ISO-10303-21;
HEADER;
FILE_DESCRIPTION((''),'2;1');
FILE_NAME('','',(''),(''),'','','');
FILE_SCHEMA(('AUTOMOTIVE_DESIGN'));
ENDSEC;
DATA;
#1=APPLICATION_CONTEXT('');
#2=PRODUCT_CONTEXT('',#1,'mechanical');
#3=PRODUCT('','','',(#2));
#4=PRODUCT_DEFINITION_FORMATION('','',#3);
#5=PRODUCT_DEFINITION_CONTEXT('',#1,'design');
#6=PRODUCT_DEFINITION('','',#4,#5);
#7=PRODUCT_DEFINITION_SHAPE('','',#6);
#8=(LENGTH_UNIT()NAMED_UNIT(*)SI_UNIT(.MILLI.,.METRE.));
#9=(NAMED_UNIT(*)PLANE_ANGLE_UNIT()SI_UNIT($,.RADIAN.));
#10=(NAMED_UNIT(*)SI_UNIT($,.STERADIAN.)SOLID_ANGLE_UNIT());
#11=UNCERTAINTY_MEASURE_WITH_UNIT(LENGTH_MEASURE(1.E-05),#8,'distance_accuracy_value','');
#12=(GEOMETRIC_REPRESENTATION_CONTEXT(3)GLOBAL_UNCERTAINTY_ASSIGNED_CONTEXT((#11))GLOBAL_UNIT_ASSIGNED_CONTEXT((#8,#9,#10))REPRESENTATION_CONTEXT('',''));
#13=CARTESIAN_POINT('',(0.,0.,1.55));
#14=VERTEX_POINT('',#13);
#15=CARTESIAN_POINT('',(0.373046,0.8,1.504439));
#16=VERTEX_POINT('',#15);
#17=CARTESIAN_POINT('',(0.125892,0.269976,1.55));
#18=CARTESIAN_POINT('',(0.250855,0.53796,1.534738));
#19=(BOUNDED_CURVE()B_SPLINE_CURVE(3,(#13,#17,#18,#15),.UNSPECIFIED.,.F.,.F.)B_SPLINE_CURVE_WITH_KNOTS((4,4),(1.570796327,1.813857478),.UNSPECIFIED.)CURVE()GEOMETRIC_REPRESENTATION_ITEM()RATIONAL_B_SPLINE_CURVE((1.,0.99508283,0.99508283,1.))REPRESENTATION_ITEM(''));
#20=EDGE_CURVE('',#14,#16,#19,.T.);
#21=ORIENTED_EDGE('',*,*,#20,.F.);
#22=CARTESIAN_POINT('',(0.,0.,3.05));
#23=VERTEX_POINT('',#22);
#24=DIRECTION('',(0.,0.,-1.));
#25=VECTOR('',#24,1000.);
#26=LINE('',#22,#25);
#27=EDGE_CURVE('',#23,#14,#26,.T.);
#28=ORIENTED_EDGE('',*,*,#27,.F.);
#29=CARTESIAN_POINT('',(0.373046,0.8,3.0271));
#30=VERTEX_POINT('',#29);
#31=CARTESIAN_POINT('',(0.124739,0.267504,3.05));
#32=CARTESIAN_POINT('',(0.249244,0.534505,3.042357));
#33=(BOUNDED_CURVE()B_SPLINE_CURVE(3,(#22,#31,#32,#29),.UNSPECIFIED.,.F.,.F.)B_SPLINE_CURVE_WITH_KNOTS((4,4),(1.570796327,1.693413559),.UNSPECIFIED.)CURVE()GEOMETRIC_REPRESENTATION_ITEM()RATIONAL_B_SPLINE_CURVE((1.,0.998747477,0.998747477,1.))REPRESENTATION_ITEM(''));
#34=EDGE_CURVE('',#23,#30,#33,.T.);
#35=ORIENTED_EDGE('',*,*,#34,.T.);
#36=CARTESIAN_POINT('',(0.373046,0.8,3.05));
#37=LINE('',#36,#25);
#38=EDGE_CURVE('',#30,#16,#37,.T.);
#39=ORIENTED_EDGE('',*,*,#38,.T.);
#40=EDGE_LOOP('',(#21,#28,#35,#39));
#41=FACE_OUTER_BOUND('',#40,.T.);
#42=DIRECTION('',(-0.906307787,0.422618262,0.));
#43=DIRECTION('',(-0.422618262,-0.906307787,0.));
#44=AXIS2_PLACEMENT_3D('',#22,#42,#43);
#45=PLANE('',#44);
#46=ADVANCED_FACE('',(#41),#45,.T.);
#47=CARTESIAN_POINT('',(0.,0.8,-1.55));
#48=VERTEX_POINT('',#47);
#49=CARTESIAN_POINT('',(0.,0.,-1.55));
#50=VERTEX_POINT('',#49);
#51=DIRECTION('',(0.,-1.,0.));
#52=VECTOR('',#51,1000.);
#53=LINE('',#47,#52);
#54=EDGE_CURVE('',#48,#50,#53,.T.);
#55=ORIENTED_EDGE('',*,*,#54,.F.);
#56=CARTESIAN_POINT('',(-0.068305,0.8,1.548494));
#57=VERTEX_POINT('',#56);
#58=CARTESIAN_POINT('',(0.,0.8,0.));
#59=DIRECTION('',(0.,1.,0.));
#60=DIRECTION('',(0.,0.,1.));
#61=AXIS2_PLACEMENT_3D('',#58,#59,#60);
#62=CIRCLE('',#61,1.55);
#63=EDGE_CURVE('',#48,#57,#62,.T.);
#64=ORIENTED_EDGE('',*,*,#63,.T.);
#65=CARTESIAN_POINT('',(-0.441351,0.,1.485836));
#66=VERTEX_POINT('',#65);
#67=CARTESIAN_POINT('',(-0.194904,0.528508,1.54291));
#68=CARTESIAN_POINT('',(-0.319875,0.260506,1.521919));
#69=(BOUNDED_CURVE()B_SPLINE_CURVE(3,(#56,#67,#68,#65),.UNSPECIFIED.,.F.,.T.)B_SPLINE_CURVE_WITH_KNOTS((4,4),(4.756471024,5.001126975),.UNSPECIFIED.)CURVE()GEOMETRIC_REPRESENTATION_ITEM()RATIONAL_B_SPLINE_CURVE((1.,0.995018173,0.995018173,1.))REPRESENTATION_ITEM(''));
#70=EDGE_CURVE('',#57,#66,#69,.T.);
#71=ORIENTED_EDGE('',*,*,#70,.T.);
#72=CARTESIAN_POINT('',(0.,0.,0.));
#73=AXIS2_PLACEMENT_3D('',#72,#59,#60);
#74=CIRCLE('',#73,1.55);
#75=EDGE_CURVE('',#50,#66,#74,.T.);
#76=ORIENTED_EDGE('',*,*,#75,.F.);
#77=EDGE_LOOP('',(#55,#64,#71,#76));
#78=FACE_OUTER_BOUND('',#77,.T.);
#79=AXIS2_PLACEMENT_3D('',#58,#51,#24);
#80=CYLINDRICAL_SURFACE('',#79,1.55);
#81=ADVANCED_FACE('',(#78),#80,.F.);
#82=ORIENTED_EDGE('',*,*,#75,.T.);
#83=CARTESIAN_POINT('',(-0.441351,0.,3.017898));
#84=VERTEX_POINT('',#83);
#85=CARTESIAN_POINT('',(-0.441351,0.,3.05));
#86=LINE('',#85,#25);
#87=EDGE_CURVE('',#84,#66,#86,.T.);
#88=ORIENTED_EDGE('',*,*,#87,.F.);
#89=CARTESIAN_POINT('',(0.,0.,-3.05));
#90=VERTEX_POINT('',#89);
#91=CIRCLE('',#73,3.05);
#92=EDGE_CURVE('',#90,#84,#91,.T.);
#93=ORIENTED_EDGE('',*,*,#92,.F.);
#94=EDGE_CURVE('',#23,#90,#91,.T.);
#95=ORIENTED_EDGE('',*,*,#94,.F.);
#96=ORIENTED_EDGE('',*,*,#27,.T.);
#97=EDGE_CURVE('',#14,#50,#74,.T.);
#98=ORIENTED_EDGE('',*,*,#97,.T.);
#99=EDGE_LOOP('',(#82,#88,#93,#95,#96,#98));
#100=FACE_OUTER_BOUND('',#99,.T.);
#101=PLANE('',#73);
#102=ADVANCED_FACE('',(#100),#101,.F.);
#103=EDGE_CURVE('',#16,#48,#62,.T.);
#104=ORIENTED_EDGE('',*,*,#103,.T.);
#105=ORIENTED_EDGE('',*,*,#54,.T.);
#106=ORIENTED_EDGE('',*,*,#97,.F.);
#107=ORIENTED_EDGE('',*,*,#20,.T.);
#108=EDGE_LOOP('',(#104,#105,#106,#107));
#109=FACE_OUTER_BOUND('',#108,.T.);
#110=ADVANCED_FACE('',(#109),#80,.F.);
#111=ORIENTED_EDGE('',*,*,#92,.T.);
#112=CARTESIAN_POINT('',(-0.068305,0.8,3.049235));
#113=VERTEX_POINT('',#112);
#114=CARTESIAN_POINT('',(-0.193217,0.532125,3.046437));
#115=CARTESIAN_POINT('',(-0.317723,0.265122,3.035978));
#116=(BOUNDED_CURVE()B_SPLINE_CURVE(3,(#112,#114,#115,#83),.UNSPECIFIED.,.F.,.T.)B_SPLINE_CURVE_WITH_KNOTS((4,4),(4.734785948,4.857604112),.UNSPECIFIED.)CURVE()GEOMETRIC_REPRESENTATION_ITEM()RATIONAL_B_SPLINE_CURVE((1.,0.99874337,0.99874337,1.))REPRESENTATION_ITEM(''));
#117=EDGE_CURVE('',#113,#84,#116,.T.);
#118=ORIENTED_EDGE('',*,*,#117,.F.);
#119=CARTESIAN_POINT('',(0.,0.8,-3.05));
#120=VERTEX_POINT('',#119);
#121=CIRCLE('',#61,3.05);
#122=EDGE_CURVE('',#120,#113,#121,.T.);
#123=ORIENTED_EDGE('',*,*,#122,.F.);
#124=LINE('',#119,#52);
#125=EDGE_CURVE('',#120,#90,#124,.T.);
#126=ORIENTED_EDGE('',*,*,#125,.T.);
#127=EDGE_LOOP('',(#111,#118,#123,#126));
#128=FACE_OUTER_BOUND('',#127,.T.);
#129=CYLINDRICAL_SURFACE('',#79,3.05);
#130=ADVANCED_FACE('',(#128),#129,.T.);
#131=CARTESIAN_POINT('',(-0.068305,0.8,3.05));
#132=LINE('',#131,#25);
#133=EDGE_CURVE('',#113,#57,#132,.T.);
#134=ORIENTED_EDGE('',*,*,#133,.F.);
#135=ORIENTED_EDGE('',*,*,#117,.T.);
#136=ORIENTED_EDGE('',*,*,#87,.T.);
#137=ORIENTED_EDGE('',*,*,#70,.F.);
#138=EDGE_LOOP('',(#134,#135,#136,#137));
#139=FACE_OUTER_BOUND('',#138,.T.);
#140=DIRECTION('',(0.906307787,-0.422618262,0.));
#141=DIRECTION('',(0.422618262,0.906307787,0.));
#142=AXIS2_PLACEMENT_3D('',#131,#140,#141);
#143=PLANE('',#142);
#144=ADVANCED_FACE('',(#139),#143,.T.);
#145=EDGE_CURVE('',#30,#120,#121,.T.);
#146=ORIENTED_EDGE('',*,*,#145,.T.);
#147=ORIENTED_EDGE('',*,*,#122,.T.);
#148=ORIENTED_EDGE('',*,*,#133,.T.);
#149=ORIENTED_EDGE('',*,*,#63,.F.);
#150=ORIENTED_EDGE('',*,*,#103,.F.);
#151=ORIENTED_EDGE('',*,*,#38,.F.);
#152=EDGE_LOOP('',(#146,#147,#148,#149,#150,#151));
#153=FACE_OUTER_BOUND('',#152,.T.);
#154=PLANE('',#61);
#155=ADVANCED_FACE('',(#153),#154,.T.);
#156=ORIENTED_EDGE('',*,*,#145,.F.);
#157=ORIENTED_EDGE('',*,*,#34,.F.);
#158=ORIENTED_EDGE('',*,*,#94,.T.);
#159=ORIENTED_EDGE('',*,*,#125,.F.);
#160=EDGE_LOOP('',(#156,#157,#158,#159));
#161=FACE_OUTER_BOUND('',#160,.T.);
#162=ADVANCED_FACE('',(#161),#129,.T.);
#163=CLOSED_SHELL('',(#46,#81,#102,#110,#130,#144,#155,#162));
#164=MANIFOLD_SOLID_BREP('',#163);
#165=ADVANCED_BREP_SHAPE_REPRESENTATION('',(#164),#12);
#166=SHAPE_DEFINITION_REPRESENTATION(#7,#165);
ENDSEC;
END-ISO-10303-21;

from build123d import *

# Parameters (mm, degrees)
SKETCH_1_R          = 3.05
SKETCH_1_R_2        = 1.55
EXTRUDE_1_DEPTH     = 0.8
CUT_EXTRUDE_1_DEPTH = 5.386912354


with BuildPart() as part:
    # 草图1 → 凸台-拉伸1 (new body)
    with BuildSketch(Plane(origin=(0, 0, 0), x_dir=(1, 0, 0), z_dir=(0, 1, 0))):
        with Locations(Location((0, 0, 0), (0, 0, 270))):
            Circle(SKETCH_1_R)
        with Locations(Location((0, 0, 0), (0, 0, 270))):
            Circle(SKETCH_1_R_2, mode=Mode.SUBTRACT)
    extrude(amount=EXTRUDE_1_DEPTH)

    # 草图2 → 切除-拉伸1 (cut, through all)
    with BuildSketch(Plane.XY):
        Polygon((0, 0), (0.373046127, 0.8), (-0.068305041, 0.8), (-0.441351168, 0), align=None)
    extrude(amount=CUT_EXTRUDE_1_DEPTH, mode=Mode.SUBTRACT)


solid = part.part
